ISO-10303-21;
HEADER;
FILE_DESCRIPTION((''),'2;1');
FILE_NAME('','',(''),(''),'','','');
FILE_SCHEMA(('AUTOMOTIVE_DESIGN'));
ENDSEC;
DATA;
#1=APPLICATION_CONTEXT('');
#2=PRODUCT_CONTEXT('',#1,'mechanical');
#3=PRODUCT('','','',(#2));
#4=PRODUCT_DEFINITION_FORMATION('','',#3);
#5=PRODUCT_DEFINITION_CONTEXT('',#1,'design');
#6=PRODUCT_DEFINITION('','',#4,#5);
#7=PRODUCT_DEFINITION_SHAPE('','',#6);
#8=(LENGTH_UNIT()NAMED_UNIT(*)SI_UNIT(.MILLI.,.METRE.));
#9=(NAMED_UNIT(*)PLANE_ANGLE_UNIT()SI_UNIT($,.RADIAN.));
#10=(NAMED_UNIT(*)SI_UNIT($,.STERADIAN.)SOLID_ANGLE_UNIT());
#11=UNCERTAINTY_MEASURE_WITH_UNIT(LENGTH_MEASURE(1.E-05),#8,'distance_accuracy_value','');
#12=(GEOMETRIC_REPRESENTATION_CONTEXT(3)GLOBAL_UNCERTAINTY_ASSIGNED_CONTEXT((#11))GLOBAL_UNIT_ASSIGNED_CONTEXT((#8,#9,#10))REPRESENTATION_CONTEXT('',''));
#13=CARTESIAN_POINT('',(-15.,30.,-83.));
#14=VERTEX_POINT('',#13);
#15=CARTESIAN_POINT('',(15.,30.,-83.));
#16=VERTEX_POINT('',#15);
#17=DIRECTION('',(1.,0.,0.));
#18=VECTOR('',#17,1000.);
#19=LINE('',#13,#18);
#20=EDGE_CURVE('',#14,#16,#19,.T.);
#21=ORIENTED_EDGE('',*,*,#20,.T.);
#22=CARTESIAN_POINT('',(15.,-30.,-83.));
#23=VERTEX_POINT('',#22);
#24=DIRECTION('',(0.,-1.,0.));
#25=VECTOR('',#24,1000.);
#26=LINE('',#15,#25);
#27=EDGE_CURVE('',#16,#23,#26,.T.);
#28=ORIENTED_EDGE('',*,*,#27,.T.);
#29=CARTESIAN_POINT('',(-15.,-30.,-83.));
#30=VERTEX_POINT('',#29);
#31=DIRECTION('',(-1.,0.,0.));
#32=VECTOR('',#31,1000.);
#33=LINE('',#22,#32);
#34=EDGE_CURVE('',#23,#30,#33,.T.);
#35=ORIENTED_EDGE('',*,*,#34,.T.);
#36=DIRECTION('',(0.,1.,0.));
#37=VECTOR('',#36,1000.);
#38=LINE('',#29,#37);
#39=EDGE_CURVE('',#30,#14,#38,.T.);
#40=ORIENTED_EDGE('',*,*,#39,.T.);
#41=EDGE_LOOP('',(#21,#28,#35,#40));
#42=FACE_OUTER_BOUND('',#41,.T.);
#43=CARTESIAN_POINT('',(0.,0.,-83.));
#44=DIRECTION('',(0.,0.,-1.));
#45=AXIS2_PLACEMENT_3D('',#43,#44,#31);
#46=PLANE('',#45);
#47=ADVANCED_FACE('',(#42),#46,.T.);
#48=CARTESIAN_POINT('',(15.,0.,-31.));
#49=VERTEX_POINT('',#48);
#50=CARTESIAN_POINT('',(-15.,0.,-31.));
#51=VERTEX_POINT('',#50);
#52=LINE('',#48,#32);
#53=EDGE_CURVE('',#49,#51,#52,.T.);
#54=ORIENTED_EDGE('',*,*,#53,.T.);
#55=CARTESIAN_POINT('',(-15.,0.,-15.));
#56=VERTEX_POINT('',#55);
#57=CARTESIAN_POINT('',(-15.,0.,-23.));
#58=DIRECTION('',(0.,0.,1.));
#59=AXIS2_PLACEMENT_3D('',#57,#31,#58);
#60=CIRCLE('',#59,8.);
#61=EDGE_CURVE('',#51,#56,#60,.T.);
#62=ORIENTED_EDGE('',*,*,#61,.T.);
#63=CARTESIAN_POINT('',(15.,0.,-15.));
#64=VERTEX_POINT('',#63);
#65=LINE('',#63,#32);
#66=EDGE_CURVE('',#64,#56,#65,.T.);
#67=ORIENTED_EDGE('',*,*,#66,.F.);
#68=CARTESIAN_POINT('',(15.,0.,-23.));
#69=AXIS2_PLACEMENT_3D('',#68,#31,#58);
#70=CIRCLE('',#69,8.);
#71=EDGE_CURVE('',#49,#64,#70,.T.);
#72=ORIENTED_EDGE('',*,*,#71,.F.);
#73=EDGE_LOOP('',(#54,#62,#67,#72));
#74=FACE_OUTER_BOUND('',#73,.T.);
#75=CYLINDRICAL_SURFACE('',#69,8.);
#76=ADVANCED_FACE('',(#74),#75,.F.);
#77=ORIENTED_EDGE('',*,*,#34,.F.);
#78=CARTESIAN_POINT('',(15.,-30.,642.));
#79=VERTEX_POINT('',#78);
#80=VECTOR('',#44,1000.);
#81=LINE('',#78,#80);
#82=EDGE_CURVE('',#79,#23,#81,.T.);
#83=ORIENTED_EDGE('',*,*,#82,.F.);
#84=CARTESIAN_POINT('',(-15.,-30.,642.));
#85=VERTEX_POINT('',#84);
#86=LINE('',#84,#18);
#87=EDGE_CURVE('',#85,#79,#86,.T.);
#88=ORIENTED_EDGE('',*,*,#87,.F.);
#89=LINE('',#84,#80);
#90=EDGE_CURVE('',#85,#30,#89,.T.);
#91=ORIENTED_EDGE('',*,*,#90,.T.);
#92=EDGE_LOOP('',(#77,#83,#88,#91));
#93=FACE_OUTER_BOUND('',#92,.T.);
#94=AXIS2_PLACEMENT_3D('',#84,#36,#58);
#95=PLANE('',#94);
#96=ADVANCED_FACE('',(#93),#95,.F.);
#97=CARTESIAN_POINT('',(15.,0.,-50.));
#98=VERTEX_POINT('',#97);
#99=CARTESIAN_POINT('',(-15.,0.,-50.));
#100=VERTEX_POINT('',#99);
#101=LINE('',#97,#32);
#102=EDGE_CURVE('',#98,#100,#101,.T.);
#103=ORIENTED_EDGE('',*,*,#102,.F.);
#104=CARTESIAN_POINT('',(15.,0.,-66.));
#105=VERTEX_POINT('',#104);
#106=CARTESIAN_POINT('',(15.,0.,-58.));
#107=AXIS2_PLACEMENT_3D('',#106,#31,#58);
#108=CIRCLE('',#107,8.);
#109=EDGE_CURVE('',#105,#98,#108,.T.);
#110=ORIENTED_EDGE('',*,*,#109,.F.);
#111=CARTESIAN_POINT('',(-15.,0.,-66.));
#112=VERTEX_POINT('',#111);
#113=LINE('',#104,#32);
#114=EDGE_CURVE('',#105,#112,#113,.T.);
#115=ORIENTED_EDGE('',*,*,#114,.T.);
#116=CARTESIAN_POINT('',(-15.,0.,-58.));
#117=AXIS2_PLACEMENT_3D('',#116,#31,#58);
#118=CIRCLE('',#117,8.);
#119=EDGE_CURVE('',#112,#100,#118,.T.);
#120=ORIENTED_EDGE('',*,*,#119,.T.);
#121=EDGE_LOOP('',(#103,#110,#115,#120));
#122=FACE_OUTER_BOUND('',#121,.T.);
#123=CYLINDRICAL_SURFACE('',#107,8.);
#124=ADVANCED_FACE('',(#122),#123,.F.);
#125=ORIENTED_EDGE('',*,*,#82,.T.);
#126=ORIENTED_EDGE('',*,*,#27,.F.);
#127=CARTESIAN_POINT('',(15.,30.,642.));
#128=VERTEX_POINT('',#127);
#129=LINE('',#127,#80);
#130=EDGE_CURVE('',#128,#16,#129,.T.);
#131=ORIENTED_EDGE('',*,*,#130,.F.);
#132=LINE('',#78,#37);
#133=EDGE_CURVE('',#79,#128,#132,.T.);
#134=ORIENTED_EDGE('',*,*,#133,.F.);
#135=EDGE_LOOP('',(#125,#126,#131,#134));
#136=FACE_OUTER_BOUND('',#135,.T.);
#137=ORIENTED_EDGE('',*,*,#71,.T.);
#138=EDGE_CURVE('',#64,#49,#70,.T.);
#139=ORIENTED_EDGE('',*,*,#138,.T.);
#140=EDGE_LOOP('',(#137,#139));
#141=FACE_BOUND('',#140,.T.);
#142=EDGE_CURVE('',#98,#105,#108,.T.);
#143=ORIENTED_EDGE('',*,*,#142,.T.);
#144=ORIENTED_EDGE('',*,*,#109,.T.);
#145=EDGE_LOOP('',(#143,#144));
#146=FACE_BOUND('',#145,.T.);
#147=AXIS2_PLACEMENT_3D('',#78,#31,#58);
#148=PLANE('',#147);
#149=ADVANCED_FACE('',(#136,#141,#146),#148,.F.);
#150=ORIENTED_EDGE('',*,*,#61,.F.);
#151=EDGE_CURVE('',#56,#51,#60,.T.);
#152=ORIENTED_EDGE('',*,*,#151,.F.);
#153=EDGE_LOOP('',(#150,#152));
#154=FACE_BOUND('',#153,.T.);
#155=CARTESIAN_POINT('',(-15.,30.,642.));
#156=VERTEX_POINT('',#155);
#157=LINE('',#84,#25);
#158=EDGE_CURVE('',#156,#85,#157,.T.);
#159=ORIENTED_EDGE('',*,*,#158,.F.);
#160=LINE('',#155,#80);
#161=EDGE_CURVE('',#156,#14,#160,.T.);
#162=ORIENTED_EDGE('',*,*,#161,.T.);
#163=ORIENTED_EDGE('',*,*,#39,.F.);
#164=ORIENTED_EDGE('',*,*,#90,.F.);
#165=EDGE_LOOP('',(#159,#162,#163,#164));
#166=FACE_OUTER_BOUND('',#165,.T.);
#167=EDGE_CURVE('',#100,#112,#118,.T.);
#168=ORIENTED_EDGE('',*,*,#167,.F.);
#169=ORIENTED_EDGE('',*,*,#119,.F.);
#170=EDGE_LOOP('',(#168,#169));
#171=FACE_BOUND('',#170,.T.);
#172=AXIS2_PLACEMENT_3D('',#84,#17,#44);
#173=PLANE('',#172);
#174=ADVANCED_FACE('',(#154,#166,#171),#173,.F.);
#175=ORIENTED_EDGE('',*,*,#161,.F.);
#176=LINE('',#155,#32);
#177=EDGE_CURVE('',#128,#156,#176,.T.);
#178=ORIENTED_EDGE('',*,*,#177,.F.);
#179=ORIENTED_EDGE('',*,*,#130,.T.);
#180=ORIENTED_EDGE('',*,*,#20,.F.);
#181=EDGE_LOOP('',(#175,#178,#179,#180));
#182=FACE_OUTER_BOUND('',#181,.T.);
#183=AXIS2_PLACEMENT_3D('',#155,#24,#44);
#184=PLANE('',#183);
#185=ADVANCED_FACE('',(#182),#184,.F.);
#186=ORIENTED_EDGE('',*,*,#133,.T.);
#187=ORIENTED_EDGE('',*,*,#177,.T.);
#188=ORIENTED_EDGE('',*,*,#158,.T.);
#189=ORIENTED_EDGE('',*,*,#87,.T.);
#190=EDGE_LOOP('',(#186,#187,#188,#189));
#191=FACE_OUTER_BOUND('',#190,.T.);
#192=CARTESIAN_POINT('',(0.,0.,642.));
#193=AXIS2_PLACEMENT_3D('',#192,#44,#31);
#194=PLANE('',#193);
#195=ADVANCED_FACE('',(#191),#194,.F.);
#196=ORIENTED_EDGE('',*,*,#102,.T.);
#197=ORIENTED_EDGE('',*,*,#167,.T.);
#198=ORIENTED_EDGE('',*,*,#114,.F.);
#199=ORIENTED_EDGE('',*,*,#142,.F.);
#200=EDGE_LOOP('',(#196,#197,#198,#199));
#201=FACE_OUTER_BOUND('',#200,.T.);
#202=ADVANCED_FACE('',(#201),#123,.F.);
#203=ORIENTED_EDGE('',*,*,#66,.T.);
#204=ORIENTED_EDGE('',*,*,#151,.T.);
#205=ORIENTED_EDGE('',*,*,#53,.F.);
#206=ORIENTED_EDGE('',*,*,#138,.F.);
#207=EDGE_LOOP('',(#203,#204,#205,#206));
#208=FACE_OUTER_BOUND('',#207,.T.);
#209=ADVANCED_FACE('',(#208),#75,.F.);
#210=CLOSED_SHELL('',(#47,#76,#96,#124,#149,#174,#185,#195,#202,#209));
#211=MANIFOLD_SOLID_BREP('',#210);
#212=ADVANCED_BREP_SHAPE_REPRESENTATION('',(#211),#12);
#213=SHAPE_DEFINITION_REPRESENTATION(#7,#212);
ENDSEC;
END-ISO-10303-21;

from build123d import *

# Parameters (mm, degrees)
SKETCH_1_W          = 30
SKETCH_1_H          = 60
EXTRUDE_1_DEPTH     = 642
SKETCH_2_W          = 30
SKETCH_2_H          = 60
EXTRUDE_2_DEPTH     = 83
SKETCH_3_R          = 8
CUT_EXTRUDE_1_DEPTH = 644.400341933


with BuildPart() as part:
    # 草图1 → 凸台-拉伸1 (new body)
    with BuildSketch(Plane.XY):
        Rectangle(SKETCH_1_W, SKETCH_1_H)
    extrude(amount=EXTRUDE_1_DEPTH)

    # 草图2 → 凸台-拉伸2 (add)
    with BuildSketch(Plane(origin=(0, 0, 0), x_dir=(-1, 0, 0), z_dir=(0, 0, -1))):
        Rectangle(SKETCH_2_W, SKETCH_2_H)
    extrude(amount=EXTRUDE_2_DEPTH)

    # 草图3 → 切除-拉伸1 (cut, through all)
    with BuildSketch(Plane.ZY.offset(15)):
        with Locations((-58, 0)):
            Circle(SKETCH_3_R)
        with Locations((-23, 0)):
            Circle(SKETCH_3_R)
    extrude(amount=-CUT_EXTRUDE_1_DEPTH, mode=Mode.SUBTRACT)


solid = part.part
